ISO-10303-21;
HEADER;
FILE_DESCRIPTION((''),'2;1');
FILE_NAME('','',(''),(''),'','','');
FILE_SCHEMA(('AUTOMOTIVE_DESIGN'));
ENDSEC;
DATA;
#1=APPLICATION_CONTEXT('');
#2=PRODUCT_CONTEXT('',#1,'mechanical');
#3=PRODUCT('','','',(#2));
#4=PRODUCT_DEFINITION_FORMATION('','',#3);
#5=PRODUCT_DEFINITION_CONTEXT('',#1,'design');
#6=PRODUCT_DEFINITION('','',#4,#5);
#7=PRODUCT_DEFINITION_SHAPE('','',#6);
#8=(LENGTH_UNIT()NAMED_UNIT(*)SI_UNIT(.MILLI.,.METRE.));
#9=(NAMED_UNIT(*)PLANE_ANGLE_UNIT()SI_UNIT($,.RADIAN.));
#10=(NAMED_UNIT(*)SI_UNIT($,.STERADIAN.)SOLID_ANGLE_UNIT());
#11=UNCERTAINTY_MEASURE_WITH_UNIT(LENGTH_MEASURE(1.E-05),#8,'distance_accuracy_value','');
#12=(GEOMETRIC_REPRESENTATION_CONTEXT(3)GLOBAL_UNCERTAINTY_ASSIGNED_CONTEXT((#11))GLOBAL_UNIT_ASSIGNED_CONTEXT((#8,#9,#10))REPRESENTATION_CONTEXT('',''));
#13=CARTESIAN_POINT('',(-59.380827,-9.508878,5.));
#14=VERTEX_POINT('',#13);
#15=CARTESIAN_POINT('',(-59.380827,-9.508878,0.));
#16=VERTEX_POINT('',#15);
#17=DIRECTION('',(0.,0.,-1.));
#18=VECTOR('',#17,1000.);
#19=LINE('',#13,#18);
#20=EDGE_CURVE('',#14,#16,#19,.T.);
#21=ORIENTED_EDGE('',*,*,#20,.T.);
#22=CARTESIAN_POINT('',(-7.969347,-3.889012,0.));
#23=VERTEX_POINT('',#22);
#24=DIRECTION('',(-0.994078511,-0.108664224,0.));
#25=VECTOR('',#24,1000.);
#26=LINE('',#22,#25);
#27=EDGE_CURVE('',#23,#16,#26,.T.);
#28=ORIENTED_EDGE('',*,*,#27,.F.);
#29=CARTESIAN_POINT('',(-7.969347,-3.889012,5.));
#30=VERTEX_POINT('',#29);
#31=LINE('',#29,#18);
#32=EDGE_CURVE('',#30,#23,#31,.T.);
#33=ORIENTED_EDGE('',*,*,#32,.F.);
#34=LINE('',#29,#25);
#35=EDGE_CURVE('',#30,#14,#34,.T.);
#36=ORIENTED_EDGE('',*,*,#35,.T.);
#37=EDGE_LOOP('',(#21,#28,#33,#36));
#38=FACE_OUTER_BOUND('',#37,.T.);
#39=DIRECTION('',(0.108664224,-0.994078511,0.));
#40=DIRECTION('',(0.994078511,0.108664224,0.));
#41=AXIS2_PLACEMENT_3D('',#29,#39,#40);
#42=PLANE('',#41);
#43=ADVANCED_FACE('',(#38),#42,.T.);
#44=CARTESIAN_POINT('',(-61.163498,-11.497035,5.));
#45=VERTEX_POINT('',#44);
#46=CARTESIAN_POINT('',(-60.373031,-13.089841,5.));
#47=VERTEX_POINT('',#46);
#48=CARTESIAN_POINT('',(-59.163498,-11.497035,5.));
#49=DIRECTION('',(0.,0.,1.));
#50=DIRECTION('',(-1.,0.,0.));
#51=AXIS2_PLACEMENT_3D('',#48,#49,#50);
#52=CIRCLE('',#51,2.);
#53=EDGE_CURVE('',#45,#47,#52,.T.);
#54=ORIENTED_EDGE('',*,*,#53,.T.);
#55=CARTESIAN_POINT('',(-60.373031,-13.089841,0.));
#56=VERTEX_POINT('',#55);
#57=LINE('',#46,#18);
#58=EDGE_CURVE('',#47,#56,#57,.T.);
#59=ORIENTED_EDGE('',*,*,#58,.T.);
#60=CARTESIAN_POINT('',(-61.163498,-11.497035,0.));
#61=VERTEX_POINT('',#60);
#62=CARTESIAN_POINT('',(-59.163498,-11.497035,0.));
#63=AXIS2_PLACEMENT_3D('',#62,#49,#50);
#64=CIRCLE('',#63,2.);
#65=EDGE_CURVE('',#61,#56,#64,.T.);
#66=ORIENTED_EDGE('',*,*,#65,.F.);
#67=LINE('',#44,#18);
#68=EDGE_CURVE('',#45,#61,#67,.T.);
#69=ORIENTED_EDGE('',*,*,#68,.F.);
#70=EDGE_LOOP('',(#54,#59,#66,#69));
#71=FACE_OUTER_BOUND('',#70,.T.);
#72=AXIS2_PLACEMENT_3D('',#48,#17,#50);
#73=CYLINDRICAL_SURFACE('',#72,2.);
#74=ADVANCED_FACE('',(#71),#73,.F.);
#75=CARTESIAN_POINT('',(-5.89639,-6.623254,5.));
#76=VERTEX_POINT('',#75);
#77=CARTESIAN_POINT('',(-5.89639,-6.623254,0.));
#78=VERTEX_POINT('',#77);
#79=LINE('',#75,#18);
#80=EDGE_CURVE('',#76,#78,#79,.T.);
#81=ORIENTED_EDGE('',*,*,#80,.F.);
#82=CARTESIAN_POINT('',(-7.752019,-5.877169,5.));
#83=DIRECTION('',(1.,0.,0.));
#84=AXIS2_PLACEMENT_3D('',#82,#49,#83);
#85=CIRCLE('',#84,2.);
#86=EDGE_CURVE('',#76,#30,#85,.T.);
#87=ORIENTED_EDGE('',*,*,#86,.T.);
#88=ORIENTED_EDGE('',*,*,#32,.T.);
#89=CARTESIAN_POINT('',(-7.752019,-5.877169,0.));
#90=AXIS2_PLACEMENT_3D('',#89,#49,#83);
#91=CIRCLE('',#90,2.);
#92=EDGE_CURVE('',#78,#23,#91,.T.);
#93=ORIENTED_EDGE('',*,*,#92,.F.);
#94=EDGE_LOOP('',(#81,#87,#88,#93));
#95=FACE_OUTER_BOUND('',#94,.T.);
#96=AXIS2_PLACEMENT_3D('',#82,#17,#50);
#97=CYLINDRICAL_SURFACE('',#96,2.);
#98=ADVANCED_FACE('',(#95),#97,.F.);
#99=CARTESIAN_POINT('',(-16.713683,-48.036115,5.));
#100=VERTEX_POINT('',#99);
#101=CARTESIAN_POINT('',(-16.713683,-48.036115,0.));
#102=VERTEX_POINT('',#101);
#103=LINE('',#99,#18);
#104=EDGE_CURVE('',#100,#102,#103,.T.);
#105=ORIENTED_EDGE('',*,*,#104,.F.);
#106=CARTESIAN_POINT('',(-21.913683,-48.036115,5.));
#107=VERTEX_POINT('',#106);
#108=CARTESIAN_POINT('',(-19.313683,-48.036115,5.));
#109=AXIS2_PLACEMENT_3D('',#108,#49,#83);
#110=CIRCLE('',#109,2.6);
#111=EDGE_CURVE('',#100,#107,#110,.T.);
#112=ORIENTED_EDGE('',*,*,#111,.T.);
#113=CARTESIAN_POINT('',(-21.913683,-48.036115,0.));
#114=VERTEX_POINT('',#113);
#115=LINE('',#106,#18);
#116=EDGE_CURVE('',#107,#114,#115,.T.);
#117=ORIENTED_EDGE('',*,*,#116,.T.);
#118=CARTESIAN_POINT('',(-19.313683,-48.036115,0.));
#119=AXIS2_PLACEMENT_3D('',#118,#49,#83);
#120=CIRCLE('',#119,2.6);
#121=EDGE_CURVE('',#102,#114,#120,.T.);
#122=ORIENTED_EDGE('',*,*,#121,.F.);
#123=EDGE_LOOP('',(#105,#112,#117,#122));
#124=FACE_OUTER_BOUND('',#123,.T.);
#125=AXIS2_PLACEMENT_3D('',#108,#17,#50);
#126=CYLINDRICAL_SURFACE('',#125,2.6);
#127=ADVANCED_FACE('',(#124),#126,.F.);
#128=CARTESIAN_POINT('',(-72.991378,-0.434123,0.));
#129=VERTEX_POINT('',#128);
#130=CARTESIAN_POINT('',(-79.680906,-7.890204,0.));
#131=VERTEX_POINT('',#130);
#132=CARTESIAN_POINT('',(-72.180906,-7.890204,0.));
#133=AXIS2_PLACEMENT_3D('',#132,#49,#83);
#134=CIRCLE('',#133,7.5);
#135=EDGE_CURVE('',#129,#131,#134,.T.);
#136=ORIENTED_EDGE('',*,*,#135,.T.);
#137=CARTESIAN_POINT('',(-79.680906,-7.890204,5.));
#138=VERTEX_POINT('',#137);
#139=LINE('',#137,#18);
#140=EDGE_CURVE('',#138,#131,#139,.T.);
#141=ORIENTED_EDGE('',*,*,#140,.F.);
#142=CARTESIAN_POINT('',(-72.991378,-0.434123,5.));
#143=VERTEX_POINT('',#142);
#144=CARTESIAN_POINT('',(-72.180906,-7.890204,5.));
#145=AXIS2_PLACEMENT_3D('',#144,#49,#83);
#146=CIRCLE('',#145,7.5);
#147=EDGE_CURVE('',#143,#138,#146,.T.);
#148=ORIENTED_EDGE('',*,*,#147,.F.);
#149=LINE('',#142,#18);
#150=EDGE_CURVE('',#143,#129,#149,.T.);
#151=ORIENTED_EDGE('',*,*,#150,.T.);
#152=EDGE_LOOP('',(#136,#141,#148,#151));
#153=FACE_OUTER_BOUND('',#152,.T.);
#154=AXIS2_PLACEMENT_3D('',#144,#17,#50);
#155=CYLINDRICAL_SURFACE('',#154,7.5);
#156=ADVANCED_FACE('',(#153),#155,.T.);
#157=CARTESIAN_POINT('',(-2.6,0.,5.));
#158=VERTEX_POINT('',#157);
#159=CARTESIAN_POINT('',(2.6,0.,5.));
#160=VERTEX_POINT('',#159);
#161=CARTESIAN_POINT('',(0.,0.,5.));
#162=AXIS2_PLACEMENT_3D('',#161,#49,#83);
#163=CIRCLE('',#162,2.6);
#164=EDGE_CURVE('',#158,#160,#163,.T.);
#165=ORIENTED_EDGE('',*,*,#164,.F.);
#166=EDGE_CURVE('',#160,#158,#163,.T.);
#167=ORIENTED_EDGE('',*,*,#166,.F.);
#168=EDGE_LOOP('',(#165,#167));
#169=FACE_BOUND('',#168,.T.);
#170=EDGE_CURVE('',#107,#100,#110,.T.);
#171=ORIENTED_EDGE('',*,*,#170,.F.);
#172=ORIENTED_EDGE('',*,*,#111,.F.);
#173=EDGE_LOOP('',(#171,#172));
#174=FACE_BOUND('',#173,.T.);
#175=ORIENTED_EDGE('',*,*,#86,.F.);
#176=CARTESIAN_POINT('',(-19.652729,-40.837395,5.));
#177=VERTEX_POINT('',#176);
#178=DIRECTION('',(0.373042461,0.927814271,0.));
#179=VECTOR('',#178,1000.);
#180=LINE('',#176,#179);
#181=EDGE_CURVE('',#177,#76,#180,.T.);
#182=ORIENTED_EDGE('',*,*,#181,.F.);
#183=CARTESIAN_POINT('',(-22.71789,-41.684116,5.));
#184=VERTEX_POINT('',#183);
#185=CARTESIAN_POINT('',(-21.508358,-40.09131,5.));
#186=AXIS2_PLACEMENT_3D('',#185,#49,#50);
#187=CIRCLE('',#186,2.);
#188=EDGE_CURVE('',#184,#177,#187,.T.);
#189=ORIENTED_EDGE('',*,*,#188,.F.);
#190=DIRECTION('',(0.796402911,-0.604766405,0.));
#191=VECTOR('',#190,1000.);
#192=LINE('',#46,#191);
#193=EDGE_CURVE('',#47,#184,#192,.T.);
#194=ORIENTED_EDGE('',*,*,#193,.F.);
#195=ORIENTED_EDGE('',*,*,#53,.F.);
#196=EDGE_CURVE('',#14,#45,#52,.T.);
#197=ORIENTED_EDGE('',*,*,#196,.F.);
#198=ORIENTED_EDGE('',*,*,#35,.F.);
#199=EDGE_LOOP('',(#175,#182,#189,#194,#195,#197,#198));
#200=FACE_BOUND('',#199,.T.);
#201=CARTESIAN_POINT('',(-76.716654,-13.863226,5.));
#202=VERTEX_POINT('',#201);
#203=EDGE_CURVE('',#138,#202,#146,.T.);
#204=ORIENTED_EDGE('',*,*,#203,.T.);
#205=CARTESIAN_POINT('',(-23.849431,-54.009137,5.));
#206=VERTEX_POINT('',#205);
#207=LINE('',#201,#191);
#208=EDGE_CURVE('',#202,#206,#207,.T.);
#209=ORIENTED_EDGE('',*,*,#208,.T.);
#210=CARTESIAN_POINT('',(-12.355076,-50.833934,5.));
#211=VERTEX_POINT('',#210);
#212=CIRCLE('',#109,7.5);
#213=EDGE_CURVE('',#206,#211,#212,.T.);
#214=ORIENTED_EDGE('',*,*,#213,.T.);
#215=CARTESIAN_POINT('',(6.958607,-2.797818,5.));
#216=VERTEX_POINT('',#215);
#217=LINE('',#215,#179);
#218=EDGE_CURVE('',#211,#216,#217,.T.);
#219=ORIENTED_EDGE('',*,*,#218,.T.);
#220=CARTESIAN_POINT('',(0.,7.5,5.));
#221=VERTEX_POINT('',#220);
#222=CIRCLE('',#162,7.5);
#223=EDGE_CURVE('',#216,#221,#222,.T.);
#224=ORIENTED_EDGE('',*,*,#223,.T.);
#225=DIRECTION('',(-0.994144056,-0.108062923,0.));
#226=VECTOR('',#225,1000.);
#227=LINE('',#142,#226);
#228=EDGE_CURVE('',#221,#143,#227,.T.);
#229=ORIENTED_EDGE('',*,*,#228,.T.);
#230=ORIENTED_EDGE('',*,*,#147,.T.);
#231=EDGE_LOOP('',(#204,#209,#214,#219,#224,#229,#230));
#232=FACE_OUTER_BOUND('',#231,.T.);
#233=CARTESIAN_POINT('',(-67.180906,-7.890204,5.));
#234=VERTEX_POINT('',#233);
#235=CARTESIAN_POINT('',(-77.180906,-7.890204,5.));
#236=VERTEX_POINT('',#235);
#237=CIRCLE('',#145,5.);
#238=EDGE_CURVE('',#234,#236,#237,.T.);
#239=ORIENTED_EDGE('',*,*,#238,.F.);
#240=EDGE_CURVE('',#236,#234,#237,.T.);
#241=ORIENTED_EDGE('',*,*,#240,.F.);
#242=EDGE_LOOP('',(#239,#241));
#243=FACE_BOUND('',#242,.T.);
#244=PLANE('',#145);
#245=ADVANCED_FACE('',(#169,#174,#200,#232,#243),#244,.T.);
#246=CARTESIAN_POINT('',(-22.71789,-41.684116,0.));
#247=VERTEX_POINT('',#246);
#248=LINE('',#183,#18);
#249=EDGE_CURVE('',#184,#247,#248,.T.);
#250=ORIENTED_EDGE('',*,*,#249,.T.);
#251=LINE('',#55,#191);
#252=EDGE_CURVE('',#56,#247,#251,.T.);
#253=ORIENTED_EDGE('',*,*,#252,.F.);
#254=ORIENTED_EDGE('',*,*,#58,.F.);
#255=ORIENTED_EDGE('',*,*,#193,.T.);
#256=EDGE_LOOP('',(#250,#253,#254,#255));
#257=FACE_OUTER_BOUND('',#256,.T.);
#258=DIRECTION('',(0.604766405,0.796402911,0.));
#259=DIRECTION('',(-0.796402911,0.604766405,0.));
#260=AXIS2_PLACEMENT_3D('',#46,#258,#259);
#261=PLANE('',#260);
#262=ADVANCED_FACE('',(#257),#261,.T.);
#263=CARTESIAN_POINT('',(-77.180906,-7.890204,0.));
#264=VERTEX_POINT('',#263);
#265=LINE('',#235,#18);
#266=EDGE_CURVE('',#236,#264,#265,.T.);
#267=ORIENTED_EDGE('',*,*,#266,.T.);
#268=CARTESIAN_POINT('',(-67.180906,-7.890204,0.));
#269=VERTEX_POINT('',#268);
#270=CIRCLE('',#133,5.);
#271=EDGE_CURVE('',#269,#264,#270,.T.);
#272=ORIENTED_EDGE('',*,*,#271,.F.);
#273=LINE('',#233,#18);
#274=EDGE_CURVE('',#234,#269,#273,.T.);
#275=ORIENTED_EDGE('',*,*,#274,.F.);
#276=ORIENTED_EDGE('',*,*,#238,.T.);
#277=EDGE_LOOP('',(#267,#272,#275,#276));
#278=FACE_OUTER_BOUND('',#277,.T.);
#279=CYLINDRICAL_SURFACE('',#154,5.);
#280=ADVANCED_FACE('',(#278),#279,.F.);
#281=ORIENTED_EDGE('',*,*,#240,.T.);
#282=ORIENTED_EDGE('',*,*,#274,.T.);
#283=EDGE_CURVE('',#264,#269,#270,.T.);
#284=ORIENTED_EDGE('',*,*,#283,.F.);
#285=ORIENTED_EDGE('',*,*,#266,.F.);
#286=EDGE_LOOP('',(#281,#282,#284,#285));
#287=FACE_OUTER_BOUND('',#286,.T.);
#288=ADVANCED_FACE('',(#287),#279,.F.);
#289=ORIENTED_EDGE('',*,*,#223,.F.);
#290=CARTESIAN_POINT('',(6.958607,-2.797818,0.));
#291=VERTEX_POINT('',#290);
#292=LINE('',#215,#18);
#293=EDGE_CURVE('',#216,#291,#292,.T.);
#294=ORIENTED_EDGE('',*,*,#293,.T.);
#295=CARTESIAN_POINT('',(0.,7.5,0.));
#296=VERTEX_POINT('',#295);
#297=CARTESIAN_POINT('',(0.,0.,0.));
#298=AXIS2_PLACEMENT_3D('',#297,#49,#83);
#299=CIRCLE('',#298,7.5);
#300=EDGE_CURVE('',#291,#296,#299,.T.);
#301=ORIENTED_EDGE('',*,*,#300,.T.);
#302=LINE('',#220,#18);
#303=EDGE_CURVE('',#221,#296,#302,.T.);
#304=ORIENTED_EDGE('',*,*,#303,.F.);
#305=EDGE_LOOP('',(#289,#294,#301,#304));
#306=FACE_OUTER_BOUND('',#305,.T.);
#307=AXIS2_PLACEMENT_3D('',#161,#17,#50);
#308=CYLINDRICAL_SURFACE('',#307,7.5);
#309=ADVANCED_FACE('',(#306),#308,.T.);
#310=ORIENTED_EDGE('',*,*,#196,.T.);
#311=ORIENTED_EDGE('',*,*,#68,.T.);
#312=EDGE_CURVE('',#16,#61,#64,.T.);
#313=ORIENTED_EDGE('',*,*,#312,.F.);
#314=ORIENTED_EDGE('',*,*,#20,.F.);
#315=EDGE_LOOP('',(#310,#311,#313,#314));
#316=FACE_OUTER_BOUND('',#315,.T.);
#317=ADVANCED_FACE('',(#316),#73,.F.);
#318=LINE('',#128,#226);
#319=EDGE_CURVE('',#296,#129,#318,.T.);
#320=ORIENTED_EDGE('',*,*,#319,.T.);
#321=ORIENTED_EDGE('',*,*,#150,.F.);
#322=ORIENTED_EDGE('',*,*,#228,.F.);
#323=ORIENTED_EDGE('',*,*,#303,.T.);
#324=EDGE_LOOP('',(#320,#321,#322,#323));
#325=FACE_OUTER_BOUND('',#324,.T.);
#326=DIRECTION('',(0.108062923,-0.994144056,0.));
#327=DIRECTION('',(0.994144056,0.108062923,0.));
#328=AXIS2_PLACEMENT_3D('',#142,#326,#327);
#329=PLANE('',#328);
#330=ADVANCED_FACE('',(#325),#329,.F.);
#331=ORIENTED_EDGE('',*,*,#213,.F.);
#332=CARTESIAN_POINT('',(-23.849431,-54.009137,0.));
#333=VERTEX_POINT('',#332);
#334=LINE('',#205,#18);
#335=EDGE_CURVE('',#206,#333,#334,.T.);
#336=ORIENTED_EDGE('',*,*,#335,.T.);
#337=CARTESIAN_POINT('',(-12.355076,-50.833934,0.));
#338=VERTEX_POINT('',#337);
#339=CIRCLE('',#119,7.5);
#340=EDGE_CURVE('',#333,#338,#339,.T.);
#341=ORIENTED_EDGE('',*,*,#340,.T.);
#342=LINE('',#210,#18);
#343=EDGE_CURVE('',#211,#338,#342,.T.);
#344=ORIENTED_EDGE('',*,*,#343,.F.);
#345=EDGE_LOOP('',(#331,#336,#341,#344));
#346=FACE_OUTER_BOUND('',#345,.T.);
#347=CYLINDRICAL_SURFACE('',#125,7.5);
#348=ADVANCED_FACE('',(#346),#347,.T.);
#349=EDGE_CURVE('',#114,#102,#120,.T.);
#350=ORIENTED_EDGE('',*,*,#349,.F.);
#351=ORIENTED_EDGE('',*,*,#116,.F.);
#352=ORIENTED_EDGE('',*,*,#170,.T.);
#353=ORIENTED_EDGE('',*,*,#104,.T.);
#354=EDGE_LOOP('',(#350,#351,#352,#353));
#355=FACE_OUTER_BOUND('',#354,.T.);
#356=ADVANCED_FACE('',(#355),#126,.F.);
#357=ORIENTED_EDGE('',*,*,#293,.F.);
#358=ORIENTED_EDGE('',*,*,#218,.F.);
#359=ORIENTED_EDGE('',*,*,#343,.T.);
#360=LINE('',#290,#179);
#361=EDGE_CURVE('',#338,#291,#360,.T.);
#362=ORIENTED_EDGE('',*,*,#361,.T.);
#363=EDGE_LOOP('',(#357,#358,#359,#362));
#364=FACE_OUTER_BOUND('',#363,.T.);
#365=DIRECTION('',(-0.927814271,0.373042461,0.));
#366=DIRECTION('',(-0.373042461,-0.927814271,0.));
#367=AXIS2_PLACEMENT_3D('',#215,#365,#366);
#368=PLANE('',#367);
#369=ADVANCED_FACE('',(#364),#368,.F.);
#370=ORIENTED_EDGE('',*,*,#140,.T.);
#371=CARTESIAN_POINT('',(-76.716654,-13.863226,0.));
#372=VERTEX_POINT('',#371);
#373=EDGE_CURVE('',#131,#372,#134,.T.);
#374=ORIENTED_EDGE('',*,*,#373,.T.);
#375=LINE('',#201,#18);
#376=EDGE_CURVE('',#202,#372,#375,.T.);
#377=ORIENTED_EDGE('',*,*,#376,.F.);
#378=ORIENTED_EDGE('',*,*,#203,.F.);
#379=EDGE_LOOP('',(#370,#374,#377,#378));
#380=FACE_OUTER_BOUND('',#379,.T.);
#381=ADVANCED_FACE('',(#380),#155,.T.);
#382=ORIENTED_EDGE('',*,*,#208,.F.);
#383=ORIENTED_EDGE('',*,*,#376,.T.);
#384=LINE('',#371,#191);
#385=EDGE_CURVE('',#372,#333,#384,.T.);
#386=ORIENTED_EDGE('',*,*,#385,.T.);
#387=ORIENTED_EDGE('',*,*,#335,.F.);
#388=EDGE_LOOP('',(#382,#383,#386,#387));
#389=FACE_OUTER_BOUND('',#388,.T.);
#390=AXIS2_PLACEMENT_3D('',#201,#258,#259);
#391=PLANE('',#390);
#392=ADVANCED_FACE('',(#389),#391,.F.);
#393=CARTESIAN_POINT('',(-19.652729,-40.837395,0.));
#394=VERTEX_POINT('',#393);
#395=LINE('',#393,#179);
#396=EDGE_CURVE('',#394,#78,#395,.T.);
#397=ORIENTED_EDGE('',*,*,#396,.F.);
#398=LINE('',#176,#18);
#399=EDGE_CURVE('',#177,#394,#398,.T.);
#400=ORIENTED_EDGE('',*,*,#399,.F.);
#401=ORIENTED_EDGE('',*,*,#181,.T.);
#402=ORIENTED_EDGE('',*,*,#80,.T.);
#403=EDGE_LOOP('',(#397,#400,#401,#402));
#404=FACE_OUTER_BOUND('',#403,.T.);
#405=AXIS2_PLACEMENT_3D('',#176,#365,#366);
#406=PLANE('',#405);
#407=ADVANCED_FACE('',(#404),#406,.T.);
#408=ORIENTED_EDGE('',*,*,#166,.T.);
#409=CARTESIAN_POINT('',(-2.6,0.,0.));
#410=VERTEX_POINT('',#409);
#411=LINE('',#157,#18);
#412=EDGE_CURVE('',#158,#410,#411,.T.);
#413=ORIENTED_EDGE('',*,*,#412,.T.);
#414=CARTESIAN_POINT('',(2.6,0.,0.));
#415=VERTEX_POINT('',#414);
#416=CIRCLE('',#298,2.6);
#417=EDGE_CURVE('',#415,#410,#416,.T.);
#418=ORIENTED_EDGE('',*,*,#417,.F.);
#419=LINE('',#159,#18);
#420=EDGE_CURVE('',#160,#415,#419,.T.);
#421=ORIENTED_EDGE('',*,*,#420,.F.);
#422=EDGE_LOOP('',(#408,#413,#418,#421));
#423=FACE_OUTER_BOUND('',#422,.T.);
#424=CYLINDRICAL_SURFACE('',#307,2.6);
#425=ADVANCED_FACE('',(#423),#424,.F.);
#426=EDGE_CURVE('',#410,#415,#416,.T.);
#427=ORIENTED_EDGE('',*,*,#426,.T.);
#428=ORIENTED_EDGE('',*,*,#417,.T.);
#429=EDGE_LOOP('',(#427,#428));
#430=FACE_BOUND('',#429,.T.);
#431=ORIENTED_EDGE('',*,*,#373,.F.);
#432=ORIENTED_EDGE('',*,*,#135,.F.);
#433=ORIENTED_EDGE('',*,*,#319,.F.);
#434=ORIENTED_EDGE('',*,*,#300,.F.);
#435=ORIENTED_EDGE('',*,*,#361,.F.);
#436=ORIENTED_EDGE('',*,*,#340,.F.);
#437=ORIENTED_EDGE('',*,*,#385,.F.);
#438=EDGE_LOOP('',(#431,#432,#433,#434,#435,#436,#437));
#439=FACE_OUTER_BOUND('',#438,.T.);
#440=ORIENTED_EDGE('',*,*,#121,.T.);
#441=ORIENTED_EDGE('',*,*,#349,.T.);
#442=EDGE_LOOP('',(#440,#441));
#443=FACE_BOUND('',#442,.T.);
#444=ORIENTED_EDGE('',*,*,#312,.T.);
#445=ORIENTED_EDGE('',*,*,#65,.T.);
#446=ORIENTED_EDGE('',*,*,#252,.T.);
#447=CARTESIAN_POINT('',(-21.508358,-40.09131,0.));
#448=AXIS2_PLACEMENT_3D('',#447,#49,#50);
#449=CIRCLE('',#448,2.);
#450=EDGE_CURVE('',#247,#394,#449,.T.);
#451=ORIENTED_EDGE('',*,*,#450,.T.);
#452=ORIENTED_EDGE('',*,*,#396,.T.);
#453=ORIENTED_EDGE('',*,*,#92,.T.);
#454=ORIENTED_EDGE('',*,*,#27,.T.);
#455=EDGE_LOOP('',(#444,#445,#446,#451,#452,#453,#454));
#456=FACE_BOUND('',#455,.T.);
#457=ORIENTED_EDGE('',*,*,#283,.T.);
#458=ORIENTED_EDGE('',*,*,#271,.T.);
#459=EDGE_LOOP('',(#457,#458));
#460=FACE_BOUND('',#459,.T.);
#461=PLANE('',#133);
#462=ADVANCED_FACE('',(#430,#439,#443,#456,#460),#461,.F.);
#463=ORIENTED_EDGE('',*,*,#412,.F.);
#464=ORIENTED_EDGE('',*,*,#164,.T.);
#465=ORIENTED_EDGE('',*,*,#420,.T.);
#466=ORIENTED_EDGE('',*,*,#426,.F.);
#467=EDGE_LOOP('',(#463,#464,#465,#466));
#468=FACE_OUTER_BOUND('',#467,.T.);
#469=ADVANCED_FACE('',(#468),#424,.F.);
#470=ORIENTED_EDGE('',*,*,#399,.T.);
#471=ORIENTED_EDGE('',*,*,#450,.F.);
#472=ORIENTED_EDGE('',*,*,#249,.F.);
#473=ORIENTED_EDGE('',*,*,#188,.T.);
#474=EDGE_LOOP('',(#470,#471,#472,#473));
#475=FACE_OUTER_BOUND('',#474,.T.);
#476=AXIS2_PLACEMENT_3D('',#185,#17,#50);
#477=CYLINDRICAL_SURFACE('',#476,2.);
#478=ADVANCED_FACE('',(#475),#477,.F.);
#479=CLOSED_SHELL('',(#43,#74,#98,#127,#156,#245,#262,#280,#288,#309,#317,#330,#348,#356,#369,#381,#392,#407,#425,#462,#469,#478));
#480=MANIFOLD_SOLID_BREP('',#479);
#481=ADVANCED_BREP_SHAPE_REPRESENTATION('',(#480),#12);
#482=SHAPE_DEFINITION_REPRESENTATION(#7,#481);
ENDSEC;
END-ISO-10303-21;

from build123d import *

# Parameters (mm, degrees)
SKETCH1_R           = 2.6
SKETCH1_R_2         = 5
BOSS_EXTRUDE1_DEPTH = 5


with BuildPart() as part:
    # Sketch1 → Boss-Extrude1 (new body)
    with BuildSketch(Plane.XY):
        with BuildLine():
            Line((-72.991378041, -0.434123458), (0, 7.5))
            ThreePointArc((0, 7.5), (6.214243254, 4.199188109), (6.958607035, -2.79781846))
            Line((6.958607035, -2.79781846), (-12.355075838, -50.833933534))
            ThreePointArc((-12.355075838, -50.833933534), (-17.316674975, -55.265358427), (-23.849430907, -54.009136903))
            Line((-23.849430907, -54.009136903), (-76.716654152, -13.863225709))
            ThreePointArc((-76.716654152, -13.863225709), (-79.407988086, -5.885388122), (-72.991378041, -0.434123458))
        make_face()
        Circle(SKETCH1_R, mode=Mode.SUBTRACT)
        with Locations((-19.313682873, -48.036115074)):
            Circle(SKETCH1_R, mode=Mode.SUBTRACT)
        with Locations((-72.180906117, -7.89020388)):
            Circle(SKETCH1_R_2, mode=Mode.SUBTRACT)
        with BuildLine():
            Line((-7.969347023, -3.889011646), (-59.380826719, -9.508878151))
            ThreePointArc((-59.380826719, -9.508878151), (-61.090881727, -10.963000514), (-60.373031081, -13.089840994))
            Line((-60.373031081, -13.089840994), (-22.717890398, -41.684116257))
            ThreePointArc((-22.717890398, -41.684116257), (-20.97582215, -42.019108663), (-19.652729047, -40.837395359))
            Line((-19.652729047, -40.837395359), (-5.896390033, -6.623253591))
            ThreePointArc((-5.896390033, -6.623253591), (-6.1582725, -4.668875059), (-7.969347023, -3.889011646))
        make_face(mode=Mode.SUBTRACT)
    extrude(amount=BOSS_EXTRUDE1_DEPTH)


solid = part.part
